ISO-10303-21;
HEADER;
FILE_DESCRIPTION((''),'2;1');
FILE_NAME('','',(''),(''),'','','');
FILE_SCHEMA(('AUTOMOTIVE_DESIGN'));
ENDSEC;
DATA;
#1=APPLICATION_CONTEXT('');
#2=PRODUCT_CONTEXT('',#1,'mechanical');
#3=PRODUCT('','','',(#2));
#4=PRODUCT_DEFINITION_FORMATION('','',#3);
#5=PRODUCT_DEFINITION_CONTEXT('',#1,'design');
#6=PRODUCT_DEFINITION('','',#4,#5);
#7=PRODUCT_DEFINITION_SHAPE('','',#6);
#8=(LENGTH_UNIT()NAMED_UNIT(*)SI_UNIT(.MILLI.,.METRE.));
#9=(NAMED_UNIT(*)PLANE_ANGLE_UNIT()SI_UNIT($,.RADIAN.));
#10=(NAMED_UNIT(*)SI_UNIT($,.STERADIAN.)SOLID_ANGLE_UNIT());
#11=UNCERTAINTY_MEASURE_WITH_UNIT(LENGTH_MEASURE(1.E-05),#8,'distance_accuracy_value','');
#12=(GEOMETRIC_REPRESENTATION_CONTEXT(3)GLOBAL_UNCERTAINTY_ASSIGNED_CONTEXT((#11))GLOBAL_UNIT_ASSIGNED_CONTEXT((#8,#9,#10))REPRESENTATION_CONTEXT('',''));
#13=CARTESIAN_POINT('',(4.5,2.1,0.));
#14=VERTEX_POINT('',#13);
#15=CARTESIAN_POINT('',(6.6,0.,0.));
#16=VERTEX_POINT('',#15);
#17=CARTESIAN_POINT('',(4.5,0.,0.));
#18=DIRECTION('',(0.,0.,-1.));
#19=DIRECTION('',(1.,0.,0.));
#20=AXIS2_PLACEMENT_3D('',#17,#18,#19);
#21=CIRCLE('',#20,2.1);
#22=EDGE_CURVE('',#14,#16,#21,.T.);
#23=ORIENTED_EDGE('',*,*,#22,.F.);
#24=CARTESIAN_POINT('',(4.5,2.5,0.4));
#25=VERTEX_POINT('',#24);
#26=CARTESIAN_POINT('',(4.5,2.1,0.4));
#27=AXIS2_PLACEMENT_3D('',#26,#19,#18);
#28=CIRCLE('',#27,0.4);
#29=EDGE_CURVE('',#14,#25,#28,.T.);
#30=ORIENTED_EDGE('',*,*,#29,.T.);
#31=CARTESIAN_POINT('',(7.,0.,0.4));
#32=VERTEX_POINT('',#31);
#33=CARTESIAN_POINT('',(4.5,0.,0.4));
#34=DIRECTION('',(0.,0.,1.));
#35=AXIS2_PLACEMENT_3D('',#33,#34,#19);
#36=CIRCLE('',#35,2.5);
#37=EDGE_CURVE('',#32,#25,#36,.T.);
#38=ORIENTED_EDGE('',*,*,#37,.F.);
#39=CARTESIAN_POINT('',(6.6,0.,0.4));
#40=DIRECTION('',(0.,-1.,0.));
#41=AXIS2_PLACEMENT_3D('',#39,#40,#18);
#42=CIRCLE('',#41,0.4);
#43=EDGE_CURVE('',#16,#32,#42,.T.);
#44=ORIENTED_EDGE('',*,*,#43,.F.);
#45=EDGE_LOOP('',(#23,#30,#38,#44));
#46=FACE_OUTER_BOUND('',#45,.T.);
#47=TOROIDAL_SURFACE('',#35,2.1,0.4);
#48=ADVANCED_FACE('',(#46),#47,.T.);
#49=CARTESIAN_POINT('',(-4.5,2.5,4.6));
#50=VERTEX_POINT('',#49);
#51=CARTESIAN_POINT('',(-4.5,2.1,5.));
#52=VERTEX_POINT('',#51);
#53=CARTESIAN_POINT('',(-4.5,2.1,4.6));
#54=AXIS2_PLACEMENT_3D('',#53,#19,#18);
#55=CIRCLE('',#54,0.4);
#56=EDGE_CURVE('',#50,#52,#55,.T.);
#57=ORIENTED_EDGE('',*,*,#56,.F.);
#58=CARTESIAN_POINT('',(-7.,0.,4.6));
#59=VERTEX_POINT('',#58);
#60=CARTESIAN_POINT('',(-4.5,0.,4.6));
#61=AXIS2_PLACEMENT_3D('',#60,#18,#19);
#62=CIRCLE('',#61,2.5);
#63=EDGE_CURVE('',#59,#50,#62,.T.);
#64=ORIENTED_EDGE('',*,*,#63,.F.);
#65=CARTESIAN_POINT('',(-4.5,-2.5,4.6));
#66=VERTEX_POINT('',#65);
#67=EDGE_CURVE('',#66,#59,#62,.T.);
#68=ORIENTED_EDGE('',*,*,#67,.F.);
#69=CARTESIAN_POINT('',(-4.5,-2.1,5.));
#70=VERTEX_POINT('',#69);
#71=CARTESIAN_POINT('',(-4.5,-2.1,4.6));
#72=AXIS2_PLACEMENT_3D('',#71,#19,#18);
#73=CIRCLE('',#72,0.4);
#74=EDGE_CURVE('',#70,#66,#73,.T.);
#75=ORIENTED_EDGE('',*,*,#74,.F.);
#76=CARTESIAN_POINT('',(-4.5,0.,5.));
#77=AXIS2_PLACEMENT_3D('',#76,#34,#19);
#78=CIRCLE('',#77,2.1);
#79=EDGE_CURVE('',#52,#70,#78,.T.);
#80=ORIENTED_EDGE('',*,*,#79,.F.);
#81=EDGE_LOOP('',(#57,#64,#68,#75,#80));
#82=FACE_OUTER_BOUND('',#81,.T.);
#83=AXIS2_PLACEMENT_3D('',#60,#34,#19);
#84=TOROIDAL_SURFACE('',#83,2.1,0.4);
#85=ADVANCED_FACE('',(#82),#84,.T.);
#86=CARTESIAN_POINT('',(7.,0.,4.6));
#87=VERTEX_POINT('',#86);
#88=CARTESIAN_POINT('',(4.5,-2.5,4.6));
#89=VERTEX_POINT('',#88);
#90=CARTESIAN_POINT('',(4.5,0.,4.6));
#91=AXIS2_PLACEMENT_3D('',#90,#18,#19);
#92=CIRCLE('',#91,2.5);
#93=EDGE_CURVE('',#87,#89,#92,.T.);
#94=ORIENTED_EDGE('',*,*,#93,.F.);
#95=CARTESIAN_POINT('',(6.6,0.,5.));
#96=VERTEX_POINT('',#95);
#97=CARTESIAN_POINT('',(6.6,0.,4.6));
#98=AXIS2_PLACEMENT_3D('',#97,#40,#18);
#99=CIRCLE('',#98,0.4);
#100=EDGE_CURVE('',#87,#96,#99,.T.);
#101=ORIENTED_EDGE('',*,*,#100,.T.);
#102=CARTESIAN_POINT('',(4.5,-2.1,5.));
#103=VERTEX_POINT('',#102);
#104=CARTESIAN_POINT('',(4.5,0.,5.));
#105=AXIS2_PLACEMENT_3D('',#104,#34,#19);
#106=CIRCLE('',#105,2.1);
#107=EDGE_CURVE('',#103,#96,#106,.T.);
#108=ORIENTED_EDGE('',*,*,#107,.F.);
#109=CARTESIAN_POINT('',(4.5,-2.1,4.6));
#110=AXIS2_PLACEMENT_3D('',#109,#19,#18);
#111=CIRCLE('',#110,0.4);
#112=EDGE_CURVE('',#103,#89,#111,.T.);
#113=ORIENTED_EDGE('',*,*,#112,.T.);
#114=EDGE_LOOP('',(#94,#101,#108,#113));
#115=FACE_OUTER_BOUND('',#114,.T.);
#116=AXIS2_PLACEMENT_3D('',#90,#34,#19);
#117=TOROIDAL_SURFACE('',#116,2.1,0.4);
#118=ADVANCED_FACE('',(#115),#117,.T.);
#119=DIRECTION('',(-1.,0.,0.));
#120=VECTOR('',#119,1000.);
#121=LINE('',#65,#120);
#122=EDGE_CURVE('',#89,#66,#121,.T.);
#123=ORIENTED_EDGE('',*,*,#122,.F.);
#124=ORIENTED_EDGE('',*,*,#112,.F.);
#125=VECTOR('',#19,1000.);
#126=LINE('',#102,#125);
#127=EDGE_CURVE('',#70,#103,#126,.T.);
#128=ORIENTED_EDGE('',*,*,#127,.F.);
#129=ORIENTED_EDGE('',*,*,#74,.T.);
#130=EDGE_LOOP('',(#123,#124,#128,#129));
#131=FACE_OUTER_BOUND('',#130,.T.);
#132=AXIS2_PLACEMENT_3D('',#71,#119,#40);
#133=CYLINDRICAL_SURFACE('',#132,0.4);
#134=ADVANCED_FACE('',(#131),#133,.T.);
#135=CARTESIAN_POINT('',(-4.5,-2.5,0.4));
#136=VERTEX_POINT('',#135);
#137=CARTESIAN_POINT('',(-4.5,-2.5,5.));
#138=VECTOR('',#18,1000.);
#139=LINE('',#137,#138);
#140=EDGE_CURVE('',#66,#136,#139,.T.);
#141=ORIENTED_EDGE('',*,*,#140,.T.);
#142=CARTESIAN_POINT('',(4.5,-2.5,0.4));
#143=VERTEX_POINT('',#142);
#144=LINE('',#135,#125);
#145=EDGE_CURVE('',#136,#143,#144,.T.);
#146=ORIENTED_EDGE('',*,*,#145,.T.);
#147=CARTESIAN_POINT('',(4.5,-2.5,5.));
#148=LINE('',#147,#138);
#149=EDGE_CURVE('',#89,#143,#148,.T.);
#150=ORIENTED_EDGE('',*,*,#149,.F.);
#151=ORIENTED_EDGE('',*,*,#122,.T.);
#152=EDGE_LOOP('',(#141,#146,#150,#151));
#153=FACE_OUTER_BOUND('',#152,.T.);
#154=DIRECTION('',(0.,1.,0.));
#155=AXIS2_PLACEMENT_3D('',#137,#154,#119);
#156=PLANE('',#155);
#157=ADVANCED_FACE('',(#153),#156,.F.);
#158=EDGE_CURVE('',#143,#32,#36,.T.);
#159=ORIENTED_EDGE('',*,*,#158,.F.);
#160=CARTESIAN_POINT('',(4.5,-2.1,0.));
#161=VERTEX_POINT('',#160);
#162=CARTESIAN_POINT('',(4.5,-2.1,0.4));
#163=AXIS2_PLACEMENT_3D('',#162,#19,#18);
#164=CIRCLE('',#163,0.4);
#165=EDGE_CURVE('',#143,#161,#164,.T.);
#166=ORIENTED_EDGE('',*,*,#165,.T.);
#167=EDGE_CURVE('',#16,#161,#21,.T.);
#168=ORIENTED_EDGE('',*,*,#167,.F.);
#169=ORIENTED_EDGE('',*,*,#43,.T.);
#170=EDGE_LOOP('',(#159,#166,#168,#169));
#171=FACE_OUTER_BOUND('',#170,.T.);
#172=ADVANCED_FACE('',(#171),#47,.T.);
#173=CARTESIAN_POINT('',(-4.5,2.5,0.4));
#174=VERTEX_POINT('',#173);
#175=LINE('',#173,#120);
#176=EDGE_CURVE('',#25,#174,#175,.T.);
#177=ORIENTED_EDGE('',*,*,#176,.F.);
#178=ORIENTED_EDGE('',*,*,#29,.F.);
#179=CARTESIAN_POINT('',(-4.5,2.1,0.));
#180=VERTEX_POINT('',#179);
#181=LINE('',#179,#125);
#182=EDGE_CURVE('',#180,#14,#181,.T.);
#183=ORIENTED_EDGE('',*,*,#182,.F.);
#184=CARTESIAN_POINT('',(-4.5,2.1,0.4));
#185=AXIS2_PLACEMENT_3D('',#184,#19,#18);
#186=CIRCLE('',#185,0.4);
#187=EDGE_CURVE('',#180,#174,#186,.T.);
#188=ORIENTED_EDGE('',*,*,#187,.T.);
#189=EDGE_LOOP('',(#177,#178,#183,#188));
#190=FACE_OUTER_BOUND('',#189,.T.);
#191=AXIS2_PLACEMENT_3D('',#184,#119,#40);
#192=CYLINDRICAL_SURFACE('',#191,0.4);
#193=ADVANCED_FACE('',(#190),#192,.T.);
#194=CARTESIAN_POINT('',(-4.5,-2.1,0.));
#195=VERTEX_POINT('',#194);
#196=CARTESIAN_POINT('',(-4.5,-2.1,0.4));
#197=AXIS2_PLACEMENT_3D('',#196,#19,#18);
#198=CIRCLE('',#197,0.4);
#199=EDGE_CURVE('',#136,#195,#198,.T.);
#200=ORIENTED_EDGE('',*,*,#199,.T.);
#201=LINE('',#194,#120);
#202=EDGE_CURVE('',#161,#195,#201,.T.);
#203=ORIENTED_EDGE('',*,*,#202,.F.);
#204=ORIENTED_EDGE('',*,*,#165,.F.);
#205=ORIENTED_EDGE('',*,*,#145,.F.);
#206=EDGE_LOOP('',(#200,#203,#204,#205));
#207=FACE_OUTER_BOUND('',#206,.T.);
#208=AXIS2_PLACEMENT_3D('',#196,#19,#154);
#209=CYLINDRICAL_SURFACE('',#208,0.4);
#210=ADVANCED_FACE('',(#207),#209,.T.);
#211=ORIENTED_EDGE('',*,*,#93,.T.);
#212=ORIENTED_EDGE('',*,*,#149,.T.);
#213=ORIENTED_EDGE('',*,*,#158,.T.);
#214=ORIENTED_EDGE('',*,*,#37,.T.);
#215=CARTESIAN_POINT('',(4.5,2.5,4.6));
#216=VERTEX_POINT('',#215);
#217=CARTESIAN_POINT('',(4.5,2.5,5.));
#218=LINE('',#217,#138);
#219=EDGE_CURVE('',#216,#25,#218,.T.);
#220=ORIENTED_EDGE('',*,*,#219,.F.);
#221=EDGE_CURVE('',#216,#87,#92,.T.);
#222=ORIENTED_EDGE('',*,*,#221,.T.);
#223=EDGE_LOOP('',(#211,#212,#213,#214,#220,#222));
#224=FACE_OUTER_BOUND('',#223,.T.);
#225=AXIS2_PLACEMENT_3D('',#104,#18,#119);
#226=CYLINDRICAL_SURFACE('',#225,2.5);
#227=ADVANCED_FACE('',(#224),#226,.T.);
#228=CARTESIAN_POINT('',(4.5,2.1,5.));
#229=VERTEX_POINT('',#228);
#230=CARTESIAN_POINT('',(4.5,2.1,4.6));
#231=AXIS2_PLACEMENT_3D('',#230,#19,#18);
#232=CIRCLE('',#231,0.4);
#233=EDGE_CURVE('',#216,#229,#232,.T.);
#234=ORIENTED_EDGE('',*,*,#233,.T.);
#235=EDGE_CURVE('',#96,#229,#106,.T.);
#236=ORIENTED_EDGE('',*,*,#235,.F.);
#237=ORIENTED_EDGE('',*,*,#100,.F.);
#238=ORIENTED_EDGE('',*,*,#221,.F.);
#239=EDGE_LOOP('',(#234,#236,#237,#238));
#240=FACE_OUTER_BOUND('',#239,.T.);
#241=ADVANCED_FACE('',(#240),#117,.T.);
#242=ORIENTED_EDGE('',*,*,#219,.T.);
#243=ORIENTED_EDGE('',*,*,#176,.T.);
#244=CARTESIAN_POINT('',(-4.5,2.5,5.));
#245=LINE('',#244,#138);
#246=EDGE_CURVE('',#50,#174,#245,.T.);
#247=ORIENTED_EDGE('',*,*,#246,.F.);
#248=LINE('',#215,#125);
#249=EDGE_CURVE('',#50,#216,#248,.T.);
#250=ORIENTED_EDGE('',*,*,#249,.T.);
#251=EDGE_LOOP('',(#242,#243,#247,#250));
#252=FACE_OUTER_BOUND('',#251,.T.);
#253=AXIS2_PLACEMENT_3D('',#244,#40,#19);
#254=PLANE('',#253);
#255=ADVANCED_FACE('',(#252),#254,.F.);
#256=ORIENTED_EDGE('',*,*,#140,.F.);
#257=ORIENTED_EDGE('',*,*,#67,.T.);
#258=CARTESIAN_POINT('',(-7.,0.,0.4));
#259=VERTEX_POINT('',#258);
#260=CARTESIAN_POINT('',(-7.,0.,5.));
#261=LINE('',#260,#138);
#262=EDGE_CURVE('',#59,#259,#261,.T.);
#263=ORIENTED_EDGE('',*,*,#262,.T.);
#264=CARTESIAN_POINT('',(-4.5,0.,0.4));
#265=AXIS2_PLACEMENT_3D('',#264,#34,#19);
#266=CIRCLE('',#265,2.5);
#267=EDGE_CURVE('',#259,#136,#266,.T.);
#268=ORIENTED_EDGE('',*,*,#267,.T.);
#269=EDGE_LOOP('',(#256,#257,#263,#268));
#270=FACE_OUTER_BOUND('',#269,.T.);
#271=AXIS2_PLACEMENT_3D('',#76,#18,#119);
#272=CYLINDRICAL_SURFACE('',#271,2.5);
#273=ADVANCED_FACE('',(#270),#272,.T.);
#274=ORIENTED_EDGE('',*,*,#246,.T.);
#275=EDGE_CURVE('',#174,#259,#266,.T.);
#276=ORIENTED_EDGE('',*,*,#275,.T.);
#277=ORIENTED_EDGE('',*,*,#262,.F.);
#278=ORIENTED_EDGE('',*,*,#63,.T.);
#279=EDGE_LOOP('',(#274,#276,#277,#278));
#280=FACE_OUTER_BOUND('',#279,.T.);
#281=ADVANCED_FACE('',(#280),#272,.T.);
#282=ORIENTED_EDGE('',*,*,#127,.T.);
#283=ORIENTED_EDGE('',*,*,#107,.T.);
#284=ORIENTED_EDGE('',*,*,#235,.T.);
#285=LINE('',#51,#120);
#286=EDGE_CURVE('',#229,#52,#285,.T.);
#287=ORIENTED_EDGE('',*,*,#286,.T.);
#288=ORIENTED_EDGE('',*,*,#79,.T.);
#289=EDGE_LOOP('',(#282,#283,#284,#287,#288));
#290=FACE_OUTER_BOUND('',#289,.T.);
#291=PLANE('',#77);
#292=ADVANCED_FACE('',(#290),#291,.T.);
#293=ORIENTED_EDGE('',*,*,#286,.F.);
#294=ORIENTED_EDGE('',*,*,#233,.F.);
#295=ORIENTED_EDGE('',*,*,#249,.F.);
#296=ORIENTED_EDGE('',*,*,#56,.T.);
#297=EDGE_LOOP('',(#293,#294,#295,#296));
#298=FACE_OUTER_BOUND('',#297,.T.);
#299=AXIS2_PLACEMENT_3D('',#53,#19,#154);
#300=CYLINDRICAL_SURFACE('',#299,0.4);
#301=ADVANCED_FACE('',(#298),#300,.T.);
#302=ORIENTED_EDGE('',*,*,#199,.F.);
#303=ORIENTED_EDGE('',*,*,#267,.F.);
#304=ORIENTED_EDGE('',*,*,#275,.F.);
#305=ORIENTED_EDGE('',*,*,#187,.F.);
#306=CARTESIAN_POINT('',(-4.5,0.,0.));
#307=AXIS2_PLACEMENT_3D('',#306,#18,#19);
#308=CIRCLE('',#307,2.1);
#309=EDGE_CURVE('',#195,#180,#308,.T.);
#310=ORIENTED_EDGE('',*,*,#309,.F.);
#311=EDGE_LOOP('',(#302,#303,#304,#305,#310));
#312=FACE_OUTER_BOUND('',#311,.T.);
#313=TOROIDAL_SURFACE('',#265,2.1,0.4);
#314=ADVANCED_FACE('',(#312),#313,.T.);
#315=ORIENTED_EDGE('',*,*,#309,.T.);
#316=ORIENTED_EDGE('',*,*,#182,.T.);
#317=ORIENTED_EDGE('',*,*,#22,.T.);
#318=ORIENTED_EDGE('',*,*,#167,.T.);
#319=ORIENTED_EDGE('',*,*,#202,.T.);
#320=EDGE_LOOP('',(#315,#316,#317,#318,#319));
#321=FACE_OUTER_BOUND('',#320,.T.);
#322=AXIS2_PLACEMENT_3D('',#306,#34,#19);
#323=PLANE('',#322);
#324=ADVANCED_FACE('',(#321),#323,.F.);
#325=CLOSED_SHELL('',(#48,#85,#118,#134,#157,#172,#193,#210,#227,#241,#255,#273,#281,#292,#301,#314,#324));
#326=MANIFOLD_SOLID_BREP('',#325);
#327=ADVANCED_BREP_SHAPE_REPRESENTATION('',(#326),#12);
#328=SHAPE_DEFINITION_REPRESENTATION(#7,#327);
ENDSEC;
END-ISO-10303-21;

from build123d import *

# Parameters (mm, degrees)
EXTRUDE_527_DEPTH = 5
FILLET_1_R        = 0.4


with BuildPart() as part:
    # 草图1 → Extrude 527 (new body)
    with BuildSketch(Plane.XY):
        with BuildLine():
            Line((-4.5, 2.5), (4.5, 2.5))
            ThreePointArc((4.5, 2.5), (7, 0), (4.5, -2.5))
            Line((4.5, -2.5), (-4.5, -2.5))
            ThreePointArc((-4.5, -2.5), (-7, 0), (-4.5, 2.5))
        make_face()
    extrude(amount=EXTRUDE_527_DEPTH)

    # 圆角1
    fillet_1_edges = [part.edges().sort_by_distance(p)[0] for p in [
        (7, 0, 5),
        (0, 2.5, 5),
        (-7, 0, 5),
        (0, 2.5, 0),
        (7, 0, 0),
        (0, -2.5, 0),
        (-7, 0, 0),
        (0, -2.5, 5),
    ]]
    fillet(fillet_1_edges, radius=FILLET_1_R)


solid = part.part
